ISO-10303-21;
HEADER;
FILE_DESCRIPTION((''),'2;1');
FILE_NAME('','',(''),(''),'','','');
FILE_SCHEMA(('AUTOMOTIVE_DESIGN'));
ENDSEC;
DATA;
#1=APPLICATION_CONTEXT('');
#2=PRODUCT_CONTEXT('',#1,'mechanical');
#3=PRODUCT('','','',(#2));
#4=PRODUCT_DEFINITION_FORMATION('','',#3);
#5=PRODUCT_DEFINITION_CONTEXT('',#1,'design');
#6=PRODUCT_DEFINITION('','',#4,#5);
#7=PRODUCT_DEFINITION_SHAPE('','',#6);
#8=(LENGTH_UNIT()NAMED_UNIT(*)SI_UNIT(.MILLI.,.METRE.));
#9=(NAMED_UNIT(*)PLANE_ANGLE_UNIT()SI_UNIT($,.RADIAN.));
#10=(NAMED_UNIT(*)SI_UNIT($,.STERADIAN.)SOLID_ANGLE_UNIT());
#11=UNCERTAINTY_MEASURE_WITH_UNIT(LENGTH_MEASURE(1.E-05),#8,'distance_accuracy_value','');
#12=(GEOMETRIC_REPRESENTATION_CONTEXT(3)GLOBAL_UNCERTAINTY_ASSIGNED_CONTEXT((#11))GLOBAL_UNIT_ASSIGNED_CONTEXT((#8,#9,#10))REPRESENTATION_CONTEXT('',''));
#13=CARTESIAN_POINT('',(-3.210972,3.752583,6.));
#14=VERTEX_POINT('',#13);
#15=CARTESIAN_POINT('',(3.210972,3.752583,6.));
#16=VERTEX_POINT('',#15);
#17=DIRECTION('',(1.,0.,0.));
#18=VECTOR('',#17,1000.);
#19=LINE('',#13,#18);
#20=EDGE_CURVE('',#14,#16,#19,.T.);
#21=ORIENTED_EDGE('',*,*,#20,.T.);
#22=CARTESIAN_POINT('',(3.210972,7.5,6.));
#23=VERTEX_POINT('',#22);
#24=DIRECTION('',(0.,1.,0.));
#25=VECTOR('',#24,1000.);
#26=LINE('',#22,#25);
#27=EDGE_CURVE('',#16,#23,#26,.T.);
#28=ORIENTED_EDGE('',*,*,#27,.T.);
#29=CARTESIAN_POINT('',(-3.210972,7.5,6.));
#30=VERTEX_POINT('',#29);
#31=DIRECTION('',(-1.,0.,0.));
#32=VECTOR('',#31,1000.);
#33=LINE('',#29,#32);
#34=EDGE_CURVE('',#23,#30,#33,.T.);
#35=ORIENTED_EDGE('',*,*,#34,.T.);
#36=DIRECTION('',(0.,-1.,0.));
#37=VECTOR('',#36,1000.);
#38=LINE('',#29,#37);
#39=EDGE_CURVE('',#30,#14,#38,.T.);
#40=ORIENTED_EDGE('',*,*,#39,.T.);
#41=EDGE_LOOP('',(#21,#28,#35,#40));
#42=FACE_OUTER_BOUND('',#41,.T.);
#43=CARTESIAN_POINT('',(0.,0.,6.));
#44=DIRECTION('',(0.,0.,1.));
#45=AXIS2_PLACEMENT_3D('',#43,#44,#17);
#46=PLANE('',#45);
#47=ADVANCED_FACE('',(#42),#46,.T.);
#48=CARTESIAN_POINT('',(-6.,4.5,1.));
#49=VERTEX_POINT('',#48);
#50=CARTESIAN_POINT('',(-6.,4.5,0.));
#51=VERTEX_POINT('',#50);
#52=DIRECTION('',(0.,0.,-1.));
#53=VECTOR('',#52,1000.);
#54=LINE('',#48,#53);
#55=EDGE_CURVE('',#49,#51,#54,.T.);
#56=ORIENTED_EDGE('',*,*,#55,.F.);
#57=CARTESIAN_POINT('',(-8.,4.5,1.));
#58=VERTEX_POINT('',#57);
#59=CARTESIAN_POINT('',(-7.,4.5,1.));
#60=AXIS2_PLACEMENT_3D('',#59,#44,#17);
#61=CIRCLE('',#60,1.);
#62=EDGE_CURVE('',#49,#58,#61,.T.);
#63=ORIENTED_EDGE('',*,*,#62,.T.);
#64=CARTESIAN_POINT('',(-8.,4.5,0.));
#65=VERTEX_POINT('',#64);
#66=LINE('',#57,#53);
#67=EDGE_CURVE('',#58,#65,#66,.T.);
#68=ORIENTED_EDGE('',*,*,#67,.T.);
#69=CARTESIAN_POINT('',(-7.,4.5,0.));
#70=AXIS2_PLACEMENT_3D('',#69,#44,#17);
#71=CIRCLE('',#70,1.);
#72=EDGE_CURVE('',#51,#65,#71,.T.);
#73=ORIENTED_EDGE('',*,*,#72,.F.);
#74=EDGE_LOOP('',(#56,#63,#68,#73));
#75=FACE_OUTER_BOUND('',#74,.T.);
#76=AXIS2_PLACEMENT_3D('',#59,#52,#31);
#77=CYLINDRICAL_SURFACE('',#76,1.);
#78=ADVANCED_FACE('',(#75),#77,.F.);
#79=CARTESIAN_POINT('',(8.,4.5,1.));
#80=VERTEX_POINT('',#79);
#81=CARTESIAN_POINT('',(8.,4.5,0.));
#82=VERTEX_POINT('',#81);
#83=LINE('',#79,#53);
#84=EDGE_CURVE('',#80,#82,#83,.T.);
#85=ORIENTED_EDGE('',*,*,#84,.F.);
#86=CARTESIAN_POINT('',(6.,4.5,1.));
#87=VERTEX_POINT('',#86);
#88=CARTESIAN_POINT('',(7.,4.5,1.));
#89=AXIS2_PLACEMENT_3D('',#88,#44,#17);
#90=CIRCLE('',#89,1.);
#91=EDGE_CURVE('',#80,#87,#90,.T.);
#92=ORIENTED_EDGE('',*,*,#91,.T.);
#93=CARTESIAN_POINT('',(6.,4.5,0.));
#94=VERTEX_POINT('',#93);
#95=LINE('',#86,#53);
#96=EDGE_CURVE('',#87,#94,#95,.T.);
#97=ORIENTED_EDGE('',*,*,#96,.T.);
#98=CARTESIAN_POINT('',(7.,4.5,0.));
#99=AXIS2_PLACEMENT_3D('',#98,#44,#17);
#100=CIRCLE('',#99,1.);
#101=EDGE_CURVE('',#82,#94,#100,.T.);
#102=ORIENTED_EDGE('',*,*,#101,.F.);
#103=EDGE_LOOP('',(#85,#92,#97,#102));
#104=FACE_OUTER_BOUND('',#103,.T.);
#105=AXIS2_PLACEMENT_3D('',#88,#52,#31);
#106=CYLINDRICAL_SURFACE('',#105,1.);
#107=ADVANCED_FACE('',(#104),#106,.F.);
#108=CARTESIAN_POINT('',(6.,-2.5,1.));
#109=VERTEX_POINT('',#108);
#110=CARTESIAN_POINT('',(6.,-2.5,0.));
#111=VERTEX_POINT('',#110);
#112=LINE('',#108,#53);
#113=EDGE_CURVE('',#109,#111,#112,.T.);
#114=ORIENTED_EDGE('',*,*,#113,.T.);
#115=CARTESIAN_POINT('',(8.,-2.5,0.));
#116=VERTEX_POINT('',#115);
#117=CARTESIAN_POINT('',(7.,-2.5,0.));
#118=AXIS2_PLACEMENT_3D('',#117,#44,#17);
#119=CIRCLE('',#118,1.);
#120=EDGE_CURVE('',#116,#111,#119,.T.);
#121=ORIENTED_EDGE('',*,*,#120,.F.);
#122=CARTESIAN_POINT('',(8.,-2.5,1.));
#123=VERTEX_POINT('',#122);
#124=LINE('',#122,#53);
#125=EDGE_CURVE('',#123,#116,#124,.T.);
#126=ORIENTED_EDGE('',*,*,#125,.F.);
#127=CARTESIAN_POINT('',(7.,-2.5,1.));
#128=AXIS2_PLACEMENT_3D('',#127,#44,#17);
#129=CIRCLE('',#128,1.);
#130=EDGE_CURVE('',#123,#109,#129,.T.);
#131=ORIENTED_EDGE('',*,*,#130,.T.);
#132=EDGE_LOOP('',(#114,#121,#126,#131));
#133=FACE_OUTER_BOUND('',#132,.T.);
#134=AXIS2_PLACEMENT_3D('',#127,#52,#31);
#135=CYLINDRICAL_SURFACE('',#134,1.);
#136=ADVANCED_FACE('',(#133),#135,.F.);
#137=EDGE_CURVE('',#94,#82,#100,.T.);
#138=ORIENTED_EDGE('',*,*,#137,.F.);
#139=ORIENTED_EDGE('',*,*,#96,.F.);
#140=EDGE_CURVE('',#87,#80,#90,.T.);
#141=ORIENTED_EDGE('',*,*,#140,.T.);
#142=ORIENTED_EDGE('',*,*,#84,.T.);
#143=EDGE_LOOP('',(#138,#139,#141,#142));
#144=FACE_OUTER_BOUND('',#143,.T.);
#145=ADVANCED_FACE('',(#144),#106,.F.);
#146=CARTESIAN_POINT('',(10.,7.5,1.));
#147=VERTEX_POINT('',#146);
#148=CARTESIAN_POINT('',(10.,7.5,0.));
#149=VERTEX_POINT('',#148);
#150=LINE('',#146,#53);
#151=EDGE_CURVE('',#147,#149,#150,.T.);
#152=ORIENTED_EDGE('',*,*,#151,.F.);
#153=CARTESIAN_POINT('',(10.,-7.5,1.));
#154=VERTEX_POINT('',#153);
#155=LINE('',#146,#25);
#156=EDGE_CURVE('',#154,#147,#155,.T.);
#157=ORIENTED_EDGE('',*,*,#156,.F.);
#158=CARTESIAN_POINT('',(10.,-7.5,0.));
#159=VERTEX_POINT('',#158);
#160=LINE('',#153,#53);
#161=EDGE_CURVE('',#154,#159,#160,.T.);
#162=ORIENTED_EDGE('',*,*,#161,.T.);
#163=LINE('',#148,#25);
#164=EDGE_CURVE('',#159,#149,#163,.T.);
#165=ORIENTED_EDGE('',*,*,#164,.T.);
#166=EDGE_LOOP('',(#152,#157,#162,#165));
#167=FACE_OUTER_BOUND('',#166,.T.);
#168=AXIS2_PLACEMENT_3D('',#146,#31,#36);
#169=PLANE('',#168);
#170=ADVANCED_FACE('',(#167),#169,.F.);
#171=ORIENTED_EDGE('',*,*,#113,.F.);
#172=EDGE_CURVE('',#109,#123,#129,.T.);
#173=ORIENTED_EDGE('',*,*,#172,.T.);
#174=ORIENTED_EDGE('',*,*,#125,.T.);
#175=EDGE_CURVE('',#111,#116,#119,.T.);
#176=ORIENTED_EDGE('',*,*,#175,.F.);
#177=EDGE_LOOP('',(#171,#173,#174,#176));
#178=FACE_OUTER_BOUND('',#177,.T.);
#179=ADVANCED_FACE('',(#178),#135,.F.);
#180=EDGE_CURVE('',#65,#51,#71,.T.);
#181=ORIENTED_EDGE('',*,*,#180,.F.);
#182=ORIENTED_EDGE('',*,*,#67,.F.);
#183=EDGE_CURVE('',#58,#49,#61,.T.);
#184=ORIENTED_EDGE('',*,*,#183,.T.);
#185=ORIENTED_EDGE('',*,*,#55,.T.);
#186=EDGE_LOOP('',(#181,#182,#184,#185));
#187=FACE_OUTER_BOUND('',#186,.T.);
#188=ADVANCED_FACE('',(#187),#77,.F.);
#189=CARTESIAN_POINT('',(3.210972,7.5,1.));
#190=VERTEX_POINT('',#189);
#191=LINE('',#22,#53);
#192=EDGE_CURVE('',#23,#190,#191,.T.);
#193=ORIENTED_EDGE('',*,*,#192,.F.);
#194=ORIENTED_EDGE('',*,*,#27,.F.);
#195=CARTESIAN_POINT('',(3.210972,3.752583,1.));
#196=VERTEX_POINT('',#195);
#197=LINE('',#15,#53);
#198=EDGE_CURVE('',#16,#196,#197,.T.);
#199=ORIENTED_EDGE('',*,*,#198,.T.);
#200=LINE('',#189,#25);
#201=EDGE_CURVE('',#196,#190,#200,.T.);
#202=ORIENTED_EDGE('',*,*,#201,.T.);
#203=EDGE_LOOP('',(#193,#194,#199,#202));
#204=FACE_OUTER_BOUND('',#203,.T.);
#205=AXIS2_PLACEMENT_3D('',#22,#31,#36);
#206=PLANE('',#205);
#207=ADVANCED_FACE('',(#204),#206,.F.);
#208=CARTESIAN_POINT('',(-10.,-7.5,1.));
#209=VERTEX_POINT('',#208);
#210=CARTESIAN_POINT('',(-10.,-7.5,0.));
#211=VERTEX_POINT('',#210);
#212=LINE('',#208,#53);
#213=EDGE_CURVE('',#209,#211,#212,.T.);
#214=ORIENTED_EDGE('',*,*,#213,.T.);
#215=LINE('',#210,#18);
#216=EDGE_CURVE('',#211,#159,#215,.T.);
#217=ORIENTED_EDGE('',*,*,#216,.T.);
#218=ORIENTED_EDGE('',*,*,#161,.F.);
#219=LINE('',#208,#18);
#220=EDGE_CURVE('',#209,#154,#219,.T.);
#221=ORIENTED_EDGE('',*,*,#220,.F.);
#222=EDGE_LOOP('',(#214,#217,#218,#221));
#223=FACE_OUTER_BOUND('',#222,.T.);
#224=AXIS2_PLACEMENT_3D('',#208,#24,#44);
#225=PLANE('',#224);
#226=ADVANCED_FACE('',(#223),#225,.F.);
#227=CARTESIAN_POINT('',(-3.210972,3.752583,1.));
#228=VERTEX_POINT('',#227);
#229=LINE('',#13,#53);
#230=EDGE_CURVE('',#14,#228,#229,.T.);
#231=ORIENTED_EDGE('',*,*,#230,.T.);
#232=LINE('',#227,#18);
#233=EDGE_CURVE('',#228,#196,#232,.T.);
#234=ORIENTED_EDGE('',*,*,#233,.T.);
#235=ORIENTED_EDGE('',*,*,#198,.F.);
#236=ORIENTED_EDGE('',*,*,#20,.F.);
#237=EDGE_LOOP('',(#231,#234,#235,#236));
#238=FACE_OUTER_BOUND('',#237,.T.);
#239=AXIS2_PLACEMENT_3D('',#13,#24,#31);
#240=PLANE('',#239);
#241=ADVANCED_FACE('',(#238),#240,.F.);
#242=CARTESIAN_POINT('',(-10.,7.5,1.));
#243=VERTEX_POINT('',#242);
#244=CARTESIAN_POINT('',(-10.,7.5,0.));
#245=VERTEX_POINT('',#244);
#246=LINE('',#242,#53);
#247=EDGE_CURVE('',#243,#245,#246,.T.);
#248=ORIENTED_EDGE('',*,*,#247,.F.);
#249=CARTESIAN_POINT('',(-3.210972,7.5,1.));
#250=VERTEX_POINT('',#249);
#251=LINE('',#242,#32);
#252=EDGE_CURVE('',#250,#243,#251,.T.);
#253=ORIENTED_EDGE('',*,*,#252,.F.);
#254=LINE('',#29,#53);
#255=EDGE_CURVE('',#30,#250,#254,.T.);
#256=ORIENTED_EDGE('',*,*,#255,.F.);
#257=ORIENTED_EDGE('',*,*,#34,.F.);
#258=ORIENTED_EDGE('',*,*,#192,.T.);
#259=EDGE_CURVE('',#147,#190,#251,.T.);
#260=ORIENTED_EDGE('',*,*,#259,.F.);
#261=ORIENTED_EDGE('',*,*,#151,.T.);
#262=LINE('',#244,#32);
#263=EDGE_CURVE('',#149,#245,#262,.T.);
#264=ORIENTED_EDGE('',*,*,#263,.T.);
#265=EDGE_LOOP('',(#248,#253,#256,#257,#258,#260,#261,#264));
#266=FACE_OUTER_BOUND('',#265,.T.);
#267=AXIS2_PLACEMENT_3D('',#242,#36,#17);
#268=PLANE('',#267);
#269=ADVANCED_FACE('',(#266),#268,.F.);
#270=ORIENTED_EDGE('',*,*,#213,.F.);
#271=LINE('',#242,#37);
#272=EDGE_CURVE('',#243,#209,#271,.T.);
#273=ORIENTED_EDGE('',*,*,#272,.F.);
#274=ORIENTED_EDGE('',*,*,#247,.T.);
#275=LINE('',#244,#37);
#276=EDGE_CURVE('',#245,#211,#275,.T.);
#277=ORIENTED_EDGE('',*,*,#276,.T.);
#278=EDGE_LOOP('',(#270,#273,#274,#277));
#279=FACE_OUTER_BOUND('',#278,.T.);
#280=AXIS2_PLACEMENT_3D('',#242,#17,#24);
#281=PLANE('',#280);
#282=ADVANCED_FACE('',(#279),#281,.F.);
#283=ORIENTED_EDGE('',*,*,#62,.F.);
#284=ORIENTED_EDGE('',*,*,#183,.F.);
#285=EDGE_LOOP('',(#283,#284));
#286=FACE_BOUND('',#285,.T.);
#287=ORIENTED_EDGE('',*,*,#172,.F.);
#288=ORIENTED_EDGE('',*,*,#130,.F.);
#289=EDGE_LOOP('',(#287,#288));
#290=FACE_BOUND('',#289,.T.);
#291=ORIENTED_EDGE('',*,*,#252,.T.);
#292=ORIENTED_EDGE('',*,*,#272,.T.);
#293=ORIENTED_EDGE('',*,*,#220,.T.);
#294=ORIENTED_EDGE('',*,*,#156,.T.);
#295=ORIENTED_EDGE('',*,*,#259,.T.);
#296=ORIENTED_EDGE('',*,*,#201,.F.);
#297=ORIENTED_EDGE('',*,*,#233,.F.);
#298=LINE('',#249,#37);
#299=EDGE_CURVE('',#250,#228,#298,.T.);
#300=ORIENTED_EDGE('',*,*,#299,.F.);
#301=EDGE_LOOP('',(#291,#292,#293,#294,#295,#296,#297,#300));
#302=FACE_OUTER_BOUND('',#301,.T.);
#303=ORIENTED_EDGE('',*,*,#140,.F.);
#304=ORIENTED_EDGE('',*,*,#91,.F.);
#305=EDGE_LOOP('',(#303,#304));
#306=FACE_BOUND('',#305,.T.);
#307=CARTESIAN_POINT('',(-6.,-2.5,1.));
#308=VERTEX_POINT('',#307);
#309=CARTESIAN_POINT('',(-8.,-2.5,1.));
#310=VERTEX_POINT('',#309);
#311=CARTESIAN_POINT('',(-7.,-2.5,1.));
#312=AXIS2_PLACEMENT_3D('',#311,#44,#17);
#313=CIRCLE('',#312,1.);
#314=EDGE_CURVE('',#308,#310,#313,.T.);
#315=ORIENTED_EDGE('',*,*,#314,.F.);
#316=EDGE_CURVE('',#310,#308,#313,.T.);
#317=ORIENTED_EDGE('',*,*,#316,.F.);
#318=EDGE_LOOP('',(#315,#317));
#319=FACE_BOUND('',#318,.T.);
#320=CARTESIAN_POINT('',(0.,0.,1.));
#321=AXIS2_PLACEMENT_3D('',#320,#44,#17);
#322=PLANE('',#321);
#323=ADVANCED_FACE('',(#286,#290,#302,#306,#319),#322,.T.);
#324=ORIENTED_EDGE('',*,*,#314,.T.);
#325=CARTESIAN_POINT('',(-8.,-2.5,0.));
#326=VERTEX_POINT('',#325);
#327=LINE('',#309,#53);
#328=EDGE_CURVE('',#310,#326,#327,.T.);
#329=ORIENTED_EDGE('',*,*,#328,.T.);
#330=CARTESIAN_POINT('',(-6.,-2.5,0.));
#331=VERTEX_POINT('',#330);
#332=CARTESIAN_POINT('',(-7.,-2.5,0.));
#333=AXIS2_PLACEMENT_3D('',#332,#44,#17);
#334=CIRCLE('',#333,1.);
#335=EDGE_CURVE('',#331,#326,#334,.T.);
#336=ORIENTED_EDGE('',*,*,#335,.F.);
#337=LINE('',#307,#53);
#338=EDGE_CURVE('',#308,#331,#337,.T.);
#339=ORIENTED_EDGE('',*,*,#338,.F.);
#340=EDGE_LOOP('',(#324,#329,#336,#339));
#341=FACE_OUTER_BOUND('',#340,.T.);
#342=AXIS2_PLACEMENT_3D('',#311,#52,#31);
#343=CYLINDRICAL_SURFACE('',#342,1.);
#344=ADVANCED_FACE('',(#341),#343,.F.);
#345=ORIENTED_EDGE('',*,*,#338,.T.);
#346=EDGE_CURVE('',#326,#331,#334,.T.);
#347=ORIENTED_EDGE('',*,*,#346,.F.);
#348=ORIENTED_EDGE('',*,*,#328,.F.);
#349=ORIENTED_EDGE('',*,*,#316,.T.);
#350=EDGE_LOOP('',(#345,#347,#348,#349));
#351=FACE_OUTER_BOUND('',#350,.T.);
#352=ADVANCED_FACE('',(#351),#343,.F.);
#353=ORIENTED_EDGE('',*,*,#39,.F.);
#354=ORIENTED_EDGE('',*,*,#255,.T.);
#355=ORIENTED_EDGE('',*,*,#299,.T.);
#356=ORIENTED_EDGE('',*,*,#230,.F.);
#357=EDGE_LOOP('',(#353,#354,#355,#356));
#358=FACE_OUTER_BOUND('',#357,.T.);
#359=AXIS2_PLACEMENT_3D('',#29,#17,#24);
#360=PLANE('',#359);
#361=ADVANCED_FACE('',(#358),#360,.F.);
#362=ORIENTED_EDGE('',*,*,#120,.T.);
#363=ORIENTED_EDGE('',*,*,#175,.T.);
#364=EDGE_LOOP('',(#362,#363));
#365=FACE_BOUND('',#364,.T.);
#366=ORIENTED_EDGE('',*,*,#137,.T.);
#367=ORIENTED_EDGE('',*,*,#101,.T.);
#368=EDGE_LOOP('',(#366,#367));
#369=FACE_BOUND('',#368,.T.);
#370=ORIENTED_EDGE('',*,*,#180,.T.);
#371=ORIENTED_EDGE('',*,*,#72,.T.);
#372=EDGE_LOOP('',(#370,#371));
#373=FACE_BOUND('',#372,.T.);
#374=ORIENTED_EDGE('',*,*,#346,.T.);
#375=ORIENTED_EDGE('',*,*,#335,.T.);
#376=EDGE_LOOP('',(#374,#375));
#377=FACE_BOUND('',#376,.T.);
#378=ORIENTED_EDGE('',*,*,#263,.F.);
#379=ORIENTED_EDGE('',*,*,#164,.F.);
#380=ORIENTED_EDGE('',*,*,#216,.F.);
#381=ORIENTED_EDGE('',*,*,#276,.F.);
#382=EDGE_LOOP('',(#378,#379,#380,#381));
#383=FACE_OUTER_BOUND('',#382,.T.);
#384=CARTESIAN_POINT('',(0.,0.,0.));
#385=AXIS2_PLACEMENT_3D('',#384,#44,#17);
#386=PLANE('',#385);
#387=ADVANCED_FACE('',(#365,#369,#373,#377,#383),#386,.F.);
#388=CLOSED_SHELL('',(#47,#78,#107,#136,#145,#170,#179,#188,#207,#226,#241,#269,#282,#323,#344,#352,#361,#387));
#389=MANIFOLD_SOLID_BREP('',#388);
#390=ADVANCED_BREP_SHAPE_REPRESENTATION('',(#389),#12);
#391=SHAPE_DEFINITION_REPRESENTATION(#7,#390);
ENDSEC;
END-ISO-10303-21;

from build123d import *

# Parameters (mm, degrees)
SKETCH1_W           = 20
SKETCH1_H           = 15
SKETCH1_R           = 1
BOSS_EXTRUDE1_DEPTH = 1
SKETCH2_W           = 6.421944946
SKETCH2_H           = 3.747416962
BOSS_EXTRUDE2_DEPTH = 5


with BuildPart() as part:
    # Sketch1 → Boss-Extrude1 (new body)
    with BuildSketch(Plane.XY):
        Rectangle(SKETCH1_W, SKETCH1_H)
        with Locations((-7, 4.5)):
            Circle(SKETCH1_R, mode=Mode.SUBTRACT)
        with Locations((-7, -2.5)):
            Circle(SKETCH1_R, mode=Mode.SUBTRACT)
        with Locations((7, 4.5)):
            Circle(SKETCH1_R, mode=Mode.SUBTRACT)
        with Locations((7, -2.5)):
            Circle(SKETCH1_R, mode=Mode.SUBTRACT)
    extrude(amount=BOSS_EXTRUDE1_DEPTH)

    # Sketch2 → Boss-Extrude2 (add)
    with BuildSketch(Plane.XY.offset(1)):
        with Locations((0, 5.626291519)):
            Rectangle(SKETCH2_W, SKETCH2_H)
    extrude(amount=BOSS_EXTRUDE2_DEPTH)


solid = part.part
